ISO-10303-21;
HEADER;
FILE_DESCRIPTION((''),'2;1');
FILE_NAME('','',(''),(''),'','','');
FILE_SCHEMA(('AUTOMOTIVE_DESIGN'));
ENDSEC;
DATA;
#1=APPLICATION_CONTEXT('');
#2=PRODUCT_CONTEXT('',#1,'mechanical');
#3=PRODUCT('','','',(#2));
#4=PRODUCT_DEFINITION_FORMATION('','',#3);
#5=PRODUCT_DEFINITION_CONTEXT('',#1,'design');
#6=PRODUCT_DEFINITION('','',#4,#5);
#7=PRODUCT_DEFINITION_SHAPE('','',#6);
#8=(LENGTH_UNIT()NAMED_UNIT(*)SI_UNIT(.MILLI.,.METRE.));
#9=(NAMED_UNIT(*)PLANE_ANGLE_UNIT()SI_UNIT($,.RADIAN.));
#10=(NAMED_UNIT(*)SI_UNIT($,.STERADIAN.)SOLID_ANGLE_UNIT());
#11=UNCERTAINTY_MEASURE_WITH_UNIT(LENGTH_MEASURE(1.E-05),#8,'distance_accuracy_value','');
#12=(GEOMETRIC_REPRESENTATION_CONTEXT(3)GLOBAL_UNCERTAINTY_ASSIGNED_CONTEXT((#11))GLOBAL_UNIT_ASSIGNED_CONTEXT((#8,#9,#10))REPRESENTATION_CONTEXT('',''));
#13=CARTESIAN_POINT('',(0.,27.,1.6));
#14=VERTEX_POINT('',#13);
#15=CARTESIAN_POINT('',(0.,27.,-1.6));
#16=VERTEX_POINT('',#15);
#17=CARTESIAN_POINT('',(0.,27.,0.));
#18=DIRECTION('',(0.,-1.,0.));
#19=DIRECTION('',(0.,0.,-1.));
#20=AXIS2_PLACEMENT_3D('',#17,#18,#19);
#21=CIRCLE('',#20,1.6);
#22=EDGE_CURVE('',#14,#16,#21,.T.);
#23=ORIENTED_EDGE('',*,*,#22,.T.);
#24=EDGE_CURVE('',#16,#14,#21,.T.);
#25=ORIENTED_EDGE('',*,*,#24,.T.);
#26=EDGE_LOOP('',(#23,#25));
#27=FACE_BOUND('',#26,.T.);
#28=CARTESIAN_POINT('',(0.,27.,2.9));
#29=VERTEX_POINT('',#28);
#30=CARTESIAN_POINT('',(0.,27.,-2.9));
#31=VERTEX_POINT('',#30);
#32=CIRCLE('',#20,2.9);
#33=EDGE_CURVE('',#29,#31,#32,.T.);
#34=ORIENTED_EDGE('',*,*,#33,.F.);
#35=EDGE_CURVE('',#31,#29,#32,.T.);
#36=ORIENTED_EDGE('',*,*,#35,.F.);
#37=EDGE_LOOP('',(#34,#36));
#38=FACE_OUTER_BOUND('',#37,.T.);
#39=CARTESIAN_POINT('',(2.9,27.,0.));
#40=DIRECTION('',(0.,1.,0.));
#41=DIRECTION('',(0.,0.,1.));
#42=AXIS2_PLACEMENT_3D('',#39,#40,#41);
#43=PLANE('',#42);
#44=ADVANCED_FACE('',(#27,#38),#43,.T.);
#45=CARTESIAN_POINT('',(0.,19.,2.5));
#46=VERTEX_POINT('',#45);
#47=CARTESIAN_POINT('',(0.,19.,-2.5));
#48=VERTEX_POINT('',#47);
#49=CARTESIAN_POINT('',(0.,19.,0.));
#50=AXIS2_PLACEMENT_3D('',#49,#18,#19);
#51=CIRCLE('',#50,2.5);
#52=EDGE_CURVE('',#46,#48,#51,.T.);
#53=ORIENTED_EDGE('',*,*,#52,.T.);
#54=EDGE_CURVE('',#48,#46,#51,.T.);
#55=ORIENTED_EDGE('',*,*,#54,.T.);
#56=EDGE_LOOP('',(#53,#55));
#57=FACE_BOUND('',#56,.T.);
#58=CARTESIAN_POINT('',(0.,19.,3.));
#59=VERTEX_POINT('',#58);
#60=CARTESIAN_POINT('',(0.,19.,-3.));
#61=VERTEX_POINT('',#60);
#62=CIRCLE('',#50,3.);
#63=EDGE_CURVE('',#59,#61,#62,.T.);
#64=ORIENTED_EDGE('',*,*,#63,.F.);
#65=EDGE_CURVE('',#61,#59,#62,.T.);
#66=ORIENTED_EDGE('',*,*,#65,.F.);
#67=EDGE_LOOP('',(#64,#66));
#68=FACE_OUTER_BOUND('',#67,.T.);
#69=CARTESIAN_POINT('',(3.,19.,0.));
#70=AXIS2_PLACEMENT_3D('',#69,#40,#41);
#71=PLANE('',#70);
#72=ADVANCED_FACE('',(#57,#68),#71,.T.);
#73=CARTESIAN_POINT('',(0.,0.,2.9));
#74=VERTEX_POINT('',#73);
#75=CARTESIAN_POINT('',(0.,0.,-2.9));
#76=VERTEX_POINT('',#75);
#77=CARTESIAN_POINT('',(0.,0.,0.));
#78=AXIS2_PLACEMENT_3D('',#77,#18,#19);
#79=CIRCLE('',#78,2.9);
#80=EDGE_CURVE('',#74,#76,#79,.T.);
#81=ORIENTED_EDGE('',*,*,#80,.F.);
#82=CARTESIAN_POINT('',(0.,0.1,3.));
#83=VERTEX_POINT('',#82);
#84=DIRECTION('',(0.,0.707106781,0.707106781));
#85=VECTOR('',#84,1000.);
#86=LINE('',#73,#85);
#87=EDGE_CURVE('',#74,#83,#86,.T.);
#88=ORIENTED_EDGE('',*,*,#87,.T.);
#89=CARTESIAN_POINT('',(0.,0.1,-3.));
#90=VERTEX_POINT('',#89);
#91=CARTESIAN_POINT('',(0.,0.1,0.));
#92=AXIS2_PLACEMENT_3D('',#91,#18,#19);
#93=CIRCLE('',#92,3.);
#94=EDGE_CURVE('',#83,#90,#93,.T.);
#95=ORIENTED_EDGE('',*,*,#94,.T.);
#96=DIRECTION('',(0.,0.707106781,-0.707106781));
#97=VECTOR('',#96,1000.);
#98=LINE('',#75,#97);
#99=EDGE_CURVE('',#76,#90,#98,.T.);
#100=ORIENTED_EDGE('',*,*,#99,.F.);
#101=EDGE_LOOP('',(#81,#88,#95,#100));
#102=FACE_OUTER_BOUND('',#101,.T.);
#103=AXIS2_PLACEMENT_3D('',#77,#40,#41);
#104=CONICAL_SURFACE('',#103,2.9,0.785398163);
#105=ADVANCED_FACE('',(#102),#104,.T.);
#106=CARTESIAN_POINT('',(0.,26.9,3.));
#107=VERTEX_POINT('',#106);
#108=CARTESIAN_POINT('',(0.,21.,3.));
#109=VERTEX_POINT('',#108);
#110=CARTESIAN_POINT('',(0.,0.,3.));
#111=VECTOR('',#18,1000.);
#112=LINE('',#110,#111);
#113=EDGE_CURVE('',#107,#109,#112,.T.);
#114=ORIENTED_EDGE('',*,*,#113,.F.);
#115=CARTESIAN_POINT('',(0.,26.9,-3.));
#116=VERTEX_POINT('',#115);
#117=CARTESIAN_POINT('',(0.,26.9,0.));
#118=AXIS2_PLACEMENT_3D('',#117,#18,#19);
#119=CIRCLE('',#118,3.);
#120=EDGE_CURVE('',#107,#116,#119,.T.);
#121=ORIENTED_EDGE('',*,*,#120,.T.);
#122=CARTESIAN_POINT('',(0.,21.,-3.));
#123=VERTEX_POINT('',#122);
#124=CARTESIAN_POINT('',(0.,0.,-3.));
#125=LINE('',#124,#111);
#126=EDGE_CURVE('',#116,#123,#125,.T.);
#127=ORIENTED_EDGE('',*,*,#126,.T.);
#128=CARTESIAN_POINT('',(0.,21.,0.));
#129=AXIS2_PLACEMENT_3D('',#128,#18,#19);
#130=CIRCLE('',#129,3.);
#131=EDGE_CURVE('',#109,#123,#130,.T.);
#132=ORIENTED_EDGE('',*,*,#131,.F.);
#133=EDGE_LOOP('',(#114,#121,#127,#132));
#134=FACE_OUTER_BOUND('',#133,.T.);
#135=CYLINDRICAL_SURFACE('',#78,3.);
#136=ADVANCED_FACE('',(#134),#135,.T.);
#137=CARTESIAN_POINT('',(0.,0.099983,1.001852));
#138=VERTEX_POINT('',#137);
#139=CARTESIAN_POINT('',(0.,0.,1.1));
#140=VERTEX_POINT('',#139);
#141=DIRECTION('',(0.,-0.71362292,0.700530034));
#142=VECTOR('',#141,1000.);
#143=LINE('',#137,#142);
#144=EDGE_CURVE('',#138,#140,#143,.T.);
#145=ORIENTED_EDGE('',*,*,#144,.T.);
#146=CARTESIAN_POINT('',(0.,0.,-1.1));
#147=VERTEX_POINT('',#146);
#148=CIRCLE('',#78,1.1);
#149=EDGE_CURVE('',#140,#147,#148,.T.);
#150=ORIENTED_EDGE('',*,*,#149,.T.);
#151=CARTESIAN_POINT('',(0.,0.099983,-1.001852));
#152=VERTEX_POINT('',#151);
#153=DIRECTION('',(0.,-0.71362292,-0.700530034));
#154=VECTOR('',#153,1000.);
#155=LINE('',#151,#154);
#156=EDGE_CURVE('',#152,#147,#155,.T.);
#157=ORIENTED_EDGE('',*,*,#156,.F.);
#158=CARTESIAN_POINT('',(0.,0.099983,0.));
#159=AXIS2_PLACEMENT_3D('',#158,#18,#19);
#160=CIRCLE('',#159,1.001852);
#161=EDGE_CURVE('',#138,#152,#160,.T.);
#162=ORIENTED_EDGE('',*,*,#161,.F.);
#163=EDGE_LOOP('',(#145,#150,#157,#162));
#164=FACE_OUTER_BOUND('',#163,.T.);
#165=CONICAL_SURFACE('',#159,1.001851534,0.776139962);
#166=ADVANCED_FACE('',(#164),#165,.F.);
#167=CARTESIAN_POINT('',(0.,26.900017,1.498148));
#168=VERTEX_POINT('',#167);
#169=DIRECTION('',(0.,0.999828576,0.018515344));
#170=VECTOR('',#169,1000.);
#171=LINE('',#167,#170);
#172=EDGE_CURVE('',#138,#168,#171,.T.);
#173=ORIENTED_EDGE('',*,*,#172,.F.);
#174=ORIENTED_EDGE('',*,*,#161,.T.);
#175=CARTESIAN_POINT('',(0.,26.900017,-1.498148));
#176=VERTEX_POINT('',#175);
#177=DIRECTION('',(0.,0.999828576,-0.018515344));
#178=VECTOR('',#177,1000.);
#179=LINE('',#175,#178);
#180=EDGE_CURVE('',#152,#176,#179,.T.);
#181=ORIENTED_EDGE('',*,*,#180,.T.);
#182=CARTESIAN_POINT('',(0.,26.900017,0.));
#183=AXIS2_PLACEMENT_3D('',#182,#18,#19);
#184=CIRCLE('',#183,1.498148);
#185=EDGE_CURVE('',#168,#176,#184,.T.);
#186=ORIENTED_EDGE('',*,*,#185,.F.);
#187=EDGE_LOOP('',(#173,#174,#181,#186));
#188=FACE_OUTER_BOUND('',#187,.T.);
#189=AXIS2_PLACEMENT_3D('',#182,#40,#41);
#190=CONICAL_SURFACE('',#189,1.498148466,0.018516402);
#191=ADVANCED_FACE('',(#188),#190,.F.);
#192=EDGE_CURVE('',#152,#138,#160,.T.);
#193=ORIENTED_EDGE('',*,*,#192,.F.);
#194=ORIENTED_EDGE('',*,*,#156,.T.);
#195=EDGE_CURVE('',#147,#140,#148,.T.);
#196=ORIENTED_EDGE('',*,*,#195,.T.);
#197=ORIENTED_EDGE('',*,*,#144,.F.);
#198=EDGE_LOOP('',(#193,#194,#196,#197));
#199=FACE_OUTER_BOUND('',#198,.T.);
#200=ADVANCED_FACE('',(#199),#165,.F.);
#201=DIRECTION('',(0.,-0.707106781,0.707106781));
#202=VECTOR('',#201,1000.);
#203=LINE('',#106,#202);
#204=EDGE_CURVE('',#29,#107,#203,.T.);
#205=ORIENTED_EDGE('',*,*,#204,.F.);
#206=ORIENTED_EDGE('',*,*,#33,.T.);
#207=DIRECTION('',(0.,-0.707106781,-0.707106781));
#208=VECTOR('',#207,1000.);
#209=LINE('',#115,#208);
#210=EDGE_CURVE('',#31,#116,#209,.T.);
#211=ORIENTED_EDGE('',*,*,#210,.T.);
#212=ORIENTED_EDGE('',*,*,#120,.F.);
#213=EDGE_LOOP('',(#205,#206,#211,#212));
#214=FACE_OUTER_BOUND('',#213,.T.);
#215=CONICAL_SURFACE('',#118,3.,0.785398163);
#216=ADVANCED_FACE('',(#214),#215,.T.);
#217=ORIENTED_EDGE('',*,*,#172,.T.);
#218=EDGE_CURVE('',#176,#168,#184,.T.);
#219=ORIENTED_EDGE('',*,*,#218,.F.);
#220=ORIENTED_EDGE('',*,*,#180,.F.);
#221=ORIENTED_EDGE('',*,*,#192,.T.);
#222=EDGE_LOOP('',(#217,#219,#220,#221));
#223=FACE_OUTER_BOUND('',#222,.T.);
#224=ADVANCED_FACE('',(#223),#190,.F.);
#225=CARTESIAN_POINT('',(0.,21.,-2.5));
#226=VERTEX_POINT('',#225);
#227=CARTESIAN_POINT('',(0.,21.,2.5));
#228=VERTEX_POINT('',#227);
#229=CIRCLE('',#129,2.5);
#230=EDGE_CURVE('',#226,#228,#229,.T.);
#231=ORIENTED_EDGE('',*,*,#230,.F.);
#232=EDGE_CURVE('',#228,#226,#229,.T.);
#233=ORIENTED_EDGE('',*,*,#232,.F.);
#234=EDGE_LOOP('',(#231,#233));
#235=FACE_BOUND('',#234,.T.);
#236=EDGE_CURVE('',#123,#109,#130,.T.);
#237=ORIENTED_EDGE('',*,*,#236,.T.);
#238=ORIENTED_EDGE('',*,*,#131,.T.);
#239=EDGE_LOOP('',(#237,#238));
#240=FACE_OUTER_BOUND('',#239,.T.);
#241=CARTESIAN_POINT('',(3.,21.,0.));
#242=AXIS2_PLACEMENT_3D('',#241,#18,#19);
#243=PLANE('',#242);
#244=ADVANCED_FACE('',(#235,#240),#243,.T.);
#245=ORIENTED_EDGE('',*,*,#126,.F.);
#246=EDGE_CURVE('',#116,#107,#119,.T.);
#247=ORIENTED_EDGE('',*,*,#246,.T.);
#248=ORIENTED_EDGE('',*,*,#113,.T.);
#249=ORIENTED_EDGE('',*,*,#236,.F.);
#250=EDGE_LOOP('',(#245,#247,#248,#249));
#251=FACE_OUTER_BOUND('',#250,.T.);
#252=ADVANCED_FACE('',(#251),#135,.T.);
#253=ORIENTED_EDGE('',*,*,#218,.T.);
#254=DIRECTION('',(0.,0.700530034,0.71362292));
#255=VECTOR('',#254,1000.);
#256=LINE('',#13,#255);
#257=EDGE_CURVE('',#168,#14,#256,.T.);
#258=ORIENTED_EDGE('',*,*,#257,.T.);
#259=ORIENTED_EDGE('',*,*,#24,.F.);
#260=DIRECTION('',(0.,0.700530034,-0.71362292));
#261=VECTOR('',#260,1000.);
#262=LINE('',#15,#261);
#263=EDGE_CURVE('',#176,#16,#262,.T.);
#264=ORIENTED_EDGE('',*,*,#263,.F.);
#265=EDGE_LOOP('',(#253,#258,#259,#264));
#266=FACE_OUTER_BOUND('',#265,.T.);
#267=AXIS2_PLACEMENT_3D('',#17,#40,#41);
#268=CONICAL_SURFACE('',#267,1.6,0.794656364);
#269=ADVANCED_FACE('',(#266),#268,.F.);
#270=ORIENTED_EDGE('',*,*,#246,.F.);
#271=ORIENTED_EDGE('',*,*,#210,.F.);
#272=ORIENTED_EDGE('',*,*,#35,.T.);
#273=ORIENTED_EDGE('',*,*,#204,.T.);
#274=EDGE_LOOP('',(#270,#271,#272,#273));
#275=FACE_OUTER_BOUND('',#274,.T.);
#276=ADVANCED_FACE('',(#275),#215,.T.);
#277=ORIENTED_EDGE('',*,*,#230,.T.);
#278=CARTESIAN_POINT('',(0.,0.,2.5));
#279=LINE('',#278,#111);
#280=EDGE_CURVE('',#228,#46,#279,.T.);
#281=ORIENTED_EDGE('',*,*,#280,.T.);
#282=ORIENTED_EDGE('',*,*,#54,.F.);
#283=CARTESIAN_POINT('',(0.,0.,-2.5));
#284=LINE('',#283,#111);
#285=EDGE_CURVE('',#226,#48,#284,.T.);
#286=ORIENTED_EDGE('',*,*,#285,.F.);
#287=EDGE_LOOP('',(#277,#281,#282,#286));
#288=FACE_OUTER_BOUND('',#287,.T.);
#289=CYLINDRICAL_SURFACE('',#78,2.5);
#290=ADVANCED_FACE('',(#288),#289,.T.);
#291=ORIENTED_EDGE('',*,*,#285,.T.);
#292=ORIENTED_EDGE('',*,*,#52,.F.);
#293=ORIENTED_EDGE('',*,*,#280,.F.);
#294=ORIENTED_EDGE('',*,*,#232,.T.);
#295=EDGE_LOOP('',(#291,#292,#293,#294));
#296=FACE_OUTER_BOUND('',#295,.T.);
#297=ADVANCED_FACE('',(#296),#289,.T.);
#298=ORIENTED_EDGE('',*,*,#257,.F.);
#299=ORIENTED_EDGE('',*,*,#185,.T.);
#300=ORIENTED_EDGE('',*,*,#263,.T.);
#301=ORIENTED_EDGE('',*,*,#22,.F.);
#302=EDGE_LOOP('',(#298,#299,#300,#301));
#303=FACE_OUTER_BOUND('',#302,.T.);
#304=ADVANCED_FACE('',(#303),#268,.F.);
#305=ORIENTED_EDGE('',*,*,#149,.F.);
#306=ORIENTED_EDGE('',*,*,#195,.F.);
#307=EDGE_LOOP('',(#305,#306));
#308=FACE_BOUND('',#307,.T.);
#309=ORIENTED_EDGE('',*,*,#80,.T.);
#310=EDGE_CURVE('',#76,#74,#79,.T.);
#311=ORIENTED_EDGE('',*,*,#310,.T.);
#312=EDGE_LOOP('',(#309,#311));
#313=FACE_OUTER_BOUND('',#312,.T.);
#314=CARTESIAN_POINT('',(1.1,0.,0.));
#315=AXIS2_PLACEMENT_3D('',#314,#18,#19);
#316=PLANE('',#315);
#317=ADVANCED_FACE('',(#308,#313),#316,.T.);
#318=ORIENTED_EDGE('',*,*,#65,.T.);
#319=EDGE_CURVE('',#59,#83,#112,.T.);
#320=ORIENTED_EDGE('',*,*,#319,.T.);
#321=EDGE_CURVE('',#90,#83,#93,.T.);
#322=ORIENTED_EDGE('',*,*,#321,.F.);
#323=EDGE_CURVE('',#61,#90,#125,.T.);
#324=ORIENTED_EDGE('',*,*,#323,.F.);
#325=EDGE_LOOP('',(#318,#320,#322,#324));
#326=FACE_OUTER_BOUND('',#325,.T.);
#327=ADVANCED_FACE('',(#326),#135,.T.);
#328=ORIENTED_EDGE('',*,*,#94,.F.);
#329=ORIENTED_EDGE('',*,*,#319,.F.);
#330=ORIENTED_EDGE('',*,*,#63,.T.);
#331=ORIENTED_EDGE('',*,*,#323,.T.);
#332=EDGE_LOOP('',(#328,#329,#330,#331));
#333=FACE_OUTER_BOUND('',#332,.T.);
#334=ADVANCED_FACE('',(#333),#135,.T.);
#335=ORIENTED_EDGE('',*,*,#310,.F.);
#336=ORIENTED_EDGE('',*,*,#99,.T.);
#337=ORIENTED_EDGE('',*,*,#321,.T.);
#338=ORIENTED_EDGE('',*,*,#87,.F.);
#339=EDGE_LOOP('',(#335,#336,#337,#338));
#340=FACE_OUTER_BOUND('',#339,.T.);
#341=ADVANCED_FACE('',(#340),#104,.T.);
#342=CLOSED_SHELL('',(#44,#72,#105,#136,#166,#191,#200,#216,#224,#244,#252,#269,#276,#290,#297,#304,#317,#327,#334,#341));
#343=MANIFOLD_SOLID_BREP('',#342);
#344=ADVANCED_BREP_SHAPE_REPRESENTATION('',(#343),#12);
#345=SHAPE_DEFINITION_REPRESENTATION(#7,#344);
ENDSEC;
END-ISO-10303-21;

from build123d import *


with BuildPart() as part:
    # Sketch1 → Revolve1 (revolve)
    with BuildSketch(Plane.XY, mode=Mode.PRIVATE) as revolve1_sk:
        Polygon((1.1, 0), (2.9, 0), (3, 0.1), (3, 19), (2.5, 19), (2.5, 21), (3, 21), (3, 26.9), (2.9, 27), (1.6, 27), (1.498148466, 26.900017142), (1.001851534, 0.099982858), align=None)
    revolve(revolve1_sk.sketch.rotate(Axis((0, 0, 0), (0, 1, 0)), 90), axis=Axis((0, 0, 0), (0, 1, 0)))


solid = part.part
